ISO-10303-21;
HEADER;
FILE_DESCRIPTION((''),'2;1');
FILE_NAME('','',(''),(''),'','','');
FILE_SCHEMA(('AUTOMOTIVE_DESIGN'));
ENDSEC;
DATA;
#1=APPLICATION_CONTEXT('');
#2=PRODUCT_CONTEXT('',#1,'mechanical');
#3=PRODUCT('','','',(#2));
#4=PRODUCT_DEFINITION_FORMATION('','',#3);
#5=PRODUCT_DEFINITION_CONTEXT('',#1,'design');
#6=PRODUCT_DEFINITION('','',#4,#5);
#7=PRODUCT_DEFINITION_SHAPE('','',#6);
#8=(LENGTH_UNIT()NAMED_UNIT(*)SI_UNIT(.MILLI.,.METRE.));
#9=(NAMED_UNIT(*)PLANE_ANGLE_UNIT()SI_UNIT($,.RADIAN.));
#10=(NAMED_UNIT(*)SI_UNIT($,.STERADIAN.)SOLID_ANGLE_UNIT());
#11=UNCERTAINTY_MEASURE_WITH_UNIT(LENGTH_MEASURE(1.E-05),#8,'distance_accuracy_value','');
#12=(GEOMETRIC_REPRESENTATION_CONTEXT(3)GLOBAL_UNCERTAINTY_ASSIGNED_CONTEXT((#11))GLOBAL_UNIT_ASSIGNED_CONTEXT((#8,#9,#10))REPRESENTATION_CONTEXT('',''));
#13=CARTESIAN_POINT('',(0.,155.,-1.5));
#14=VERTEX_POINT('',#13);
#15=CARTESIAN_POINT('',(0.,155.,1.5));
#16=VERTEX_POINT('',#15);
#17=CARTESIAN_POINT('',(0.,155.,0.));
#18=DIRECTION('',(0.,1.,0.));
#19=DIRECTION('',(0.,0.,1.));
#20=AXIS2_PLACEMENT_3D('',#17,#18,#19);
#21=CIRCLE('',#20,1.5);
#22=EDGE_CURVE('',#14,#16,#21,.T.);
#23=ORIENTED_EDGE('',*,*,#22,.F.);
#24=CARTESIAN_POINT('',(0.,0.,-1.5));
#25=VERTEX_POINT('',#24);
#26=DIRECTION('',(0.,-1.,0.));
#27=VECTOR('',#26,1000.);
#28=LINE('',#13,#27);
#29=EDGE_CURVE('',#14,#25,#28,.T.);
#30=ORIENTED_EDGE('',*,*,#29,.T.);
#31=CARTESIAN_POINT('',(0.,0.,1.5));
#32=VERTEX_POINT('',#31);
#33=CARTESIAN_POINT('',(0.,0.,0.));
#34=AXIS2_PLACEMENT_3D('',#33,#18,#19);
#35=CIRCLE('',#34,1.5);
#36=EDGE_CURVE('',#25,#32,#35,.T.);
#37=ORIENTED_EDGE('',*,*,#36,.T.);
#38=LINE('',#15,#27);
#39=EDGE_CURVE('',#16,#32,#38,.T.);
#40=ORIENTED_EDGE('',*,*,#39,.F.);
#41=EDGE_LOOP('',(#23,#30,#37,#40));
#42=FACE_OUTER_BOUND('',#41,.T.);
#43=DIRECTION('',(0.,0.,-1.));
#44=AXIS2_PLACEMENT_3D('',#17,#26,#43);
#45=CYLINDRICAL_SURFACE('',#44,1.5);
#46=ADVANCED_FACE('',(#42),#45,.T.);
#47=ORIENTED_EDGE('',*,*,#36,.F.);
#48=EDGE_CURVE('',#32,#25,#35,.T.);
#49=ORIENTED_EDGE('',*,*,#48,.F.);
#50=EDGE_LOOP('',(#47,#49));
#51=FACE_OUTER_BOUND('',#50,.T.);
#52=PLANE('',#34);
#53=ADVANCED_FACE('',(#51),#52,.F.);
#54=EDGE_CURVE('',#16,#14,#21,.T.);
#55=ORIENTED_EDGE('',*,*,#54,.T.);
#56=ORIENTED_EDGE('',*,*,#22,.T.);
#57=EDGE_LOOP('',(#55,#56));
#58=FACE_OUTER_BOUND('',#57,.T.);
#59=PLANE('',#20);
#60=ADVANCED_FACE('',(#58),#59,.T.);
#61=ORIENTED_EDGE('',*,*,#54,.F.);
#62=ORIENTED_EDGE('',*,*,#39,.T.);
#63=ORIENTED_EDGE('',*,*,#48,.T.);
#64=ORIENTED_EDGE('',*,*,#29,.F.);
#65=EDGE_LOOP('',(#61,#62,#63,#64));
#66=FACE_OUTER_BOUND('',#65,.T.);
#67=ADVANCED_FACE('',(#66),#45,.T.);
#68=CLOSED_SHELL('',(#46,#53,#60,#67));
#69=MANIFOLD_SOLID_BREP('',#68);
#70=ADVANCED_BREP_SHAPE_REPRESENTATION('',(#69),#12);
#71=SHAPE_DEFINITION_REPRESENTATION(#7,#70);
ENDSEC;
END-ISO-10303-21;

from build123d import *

# Parameters (mm, degrees)
SKETCH_2_R      = 1.5
EXTRUDE_1_DEPTH = 155


with BuildPart() as part:
    # 草图2 → 凸台-拉伸1 (new body)
    with BuildSketch(Plane(origin=(0, 0, 0), x_dir=(1, 0, 0), z_dir=(0, 1, 0))):
        with Locations(Location((0, 0, 0), (0, 0, 270))):
            Circle(SKETCH_2_R)
    extrude(amount=EXTRUDE_1_DEPTH)


solid = part.part
